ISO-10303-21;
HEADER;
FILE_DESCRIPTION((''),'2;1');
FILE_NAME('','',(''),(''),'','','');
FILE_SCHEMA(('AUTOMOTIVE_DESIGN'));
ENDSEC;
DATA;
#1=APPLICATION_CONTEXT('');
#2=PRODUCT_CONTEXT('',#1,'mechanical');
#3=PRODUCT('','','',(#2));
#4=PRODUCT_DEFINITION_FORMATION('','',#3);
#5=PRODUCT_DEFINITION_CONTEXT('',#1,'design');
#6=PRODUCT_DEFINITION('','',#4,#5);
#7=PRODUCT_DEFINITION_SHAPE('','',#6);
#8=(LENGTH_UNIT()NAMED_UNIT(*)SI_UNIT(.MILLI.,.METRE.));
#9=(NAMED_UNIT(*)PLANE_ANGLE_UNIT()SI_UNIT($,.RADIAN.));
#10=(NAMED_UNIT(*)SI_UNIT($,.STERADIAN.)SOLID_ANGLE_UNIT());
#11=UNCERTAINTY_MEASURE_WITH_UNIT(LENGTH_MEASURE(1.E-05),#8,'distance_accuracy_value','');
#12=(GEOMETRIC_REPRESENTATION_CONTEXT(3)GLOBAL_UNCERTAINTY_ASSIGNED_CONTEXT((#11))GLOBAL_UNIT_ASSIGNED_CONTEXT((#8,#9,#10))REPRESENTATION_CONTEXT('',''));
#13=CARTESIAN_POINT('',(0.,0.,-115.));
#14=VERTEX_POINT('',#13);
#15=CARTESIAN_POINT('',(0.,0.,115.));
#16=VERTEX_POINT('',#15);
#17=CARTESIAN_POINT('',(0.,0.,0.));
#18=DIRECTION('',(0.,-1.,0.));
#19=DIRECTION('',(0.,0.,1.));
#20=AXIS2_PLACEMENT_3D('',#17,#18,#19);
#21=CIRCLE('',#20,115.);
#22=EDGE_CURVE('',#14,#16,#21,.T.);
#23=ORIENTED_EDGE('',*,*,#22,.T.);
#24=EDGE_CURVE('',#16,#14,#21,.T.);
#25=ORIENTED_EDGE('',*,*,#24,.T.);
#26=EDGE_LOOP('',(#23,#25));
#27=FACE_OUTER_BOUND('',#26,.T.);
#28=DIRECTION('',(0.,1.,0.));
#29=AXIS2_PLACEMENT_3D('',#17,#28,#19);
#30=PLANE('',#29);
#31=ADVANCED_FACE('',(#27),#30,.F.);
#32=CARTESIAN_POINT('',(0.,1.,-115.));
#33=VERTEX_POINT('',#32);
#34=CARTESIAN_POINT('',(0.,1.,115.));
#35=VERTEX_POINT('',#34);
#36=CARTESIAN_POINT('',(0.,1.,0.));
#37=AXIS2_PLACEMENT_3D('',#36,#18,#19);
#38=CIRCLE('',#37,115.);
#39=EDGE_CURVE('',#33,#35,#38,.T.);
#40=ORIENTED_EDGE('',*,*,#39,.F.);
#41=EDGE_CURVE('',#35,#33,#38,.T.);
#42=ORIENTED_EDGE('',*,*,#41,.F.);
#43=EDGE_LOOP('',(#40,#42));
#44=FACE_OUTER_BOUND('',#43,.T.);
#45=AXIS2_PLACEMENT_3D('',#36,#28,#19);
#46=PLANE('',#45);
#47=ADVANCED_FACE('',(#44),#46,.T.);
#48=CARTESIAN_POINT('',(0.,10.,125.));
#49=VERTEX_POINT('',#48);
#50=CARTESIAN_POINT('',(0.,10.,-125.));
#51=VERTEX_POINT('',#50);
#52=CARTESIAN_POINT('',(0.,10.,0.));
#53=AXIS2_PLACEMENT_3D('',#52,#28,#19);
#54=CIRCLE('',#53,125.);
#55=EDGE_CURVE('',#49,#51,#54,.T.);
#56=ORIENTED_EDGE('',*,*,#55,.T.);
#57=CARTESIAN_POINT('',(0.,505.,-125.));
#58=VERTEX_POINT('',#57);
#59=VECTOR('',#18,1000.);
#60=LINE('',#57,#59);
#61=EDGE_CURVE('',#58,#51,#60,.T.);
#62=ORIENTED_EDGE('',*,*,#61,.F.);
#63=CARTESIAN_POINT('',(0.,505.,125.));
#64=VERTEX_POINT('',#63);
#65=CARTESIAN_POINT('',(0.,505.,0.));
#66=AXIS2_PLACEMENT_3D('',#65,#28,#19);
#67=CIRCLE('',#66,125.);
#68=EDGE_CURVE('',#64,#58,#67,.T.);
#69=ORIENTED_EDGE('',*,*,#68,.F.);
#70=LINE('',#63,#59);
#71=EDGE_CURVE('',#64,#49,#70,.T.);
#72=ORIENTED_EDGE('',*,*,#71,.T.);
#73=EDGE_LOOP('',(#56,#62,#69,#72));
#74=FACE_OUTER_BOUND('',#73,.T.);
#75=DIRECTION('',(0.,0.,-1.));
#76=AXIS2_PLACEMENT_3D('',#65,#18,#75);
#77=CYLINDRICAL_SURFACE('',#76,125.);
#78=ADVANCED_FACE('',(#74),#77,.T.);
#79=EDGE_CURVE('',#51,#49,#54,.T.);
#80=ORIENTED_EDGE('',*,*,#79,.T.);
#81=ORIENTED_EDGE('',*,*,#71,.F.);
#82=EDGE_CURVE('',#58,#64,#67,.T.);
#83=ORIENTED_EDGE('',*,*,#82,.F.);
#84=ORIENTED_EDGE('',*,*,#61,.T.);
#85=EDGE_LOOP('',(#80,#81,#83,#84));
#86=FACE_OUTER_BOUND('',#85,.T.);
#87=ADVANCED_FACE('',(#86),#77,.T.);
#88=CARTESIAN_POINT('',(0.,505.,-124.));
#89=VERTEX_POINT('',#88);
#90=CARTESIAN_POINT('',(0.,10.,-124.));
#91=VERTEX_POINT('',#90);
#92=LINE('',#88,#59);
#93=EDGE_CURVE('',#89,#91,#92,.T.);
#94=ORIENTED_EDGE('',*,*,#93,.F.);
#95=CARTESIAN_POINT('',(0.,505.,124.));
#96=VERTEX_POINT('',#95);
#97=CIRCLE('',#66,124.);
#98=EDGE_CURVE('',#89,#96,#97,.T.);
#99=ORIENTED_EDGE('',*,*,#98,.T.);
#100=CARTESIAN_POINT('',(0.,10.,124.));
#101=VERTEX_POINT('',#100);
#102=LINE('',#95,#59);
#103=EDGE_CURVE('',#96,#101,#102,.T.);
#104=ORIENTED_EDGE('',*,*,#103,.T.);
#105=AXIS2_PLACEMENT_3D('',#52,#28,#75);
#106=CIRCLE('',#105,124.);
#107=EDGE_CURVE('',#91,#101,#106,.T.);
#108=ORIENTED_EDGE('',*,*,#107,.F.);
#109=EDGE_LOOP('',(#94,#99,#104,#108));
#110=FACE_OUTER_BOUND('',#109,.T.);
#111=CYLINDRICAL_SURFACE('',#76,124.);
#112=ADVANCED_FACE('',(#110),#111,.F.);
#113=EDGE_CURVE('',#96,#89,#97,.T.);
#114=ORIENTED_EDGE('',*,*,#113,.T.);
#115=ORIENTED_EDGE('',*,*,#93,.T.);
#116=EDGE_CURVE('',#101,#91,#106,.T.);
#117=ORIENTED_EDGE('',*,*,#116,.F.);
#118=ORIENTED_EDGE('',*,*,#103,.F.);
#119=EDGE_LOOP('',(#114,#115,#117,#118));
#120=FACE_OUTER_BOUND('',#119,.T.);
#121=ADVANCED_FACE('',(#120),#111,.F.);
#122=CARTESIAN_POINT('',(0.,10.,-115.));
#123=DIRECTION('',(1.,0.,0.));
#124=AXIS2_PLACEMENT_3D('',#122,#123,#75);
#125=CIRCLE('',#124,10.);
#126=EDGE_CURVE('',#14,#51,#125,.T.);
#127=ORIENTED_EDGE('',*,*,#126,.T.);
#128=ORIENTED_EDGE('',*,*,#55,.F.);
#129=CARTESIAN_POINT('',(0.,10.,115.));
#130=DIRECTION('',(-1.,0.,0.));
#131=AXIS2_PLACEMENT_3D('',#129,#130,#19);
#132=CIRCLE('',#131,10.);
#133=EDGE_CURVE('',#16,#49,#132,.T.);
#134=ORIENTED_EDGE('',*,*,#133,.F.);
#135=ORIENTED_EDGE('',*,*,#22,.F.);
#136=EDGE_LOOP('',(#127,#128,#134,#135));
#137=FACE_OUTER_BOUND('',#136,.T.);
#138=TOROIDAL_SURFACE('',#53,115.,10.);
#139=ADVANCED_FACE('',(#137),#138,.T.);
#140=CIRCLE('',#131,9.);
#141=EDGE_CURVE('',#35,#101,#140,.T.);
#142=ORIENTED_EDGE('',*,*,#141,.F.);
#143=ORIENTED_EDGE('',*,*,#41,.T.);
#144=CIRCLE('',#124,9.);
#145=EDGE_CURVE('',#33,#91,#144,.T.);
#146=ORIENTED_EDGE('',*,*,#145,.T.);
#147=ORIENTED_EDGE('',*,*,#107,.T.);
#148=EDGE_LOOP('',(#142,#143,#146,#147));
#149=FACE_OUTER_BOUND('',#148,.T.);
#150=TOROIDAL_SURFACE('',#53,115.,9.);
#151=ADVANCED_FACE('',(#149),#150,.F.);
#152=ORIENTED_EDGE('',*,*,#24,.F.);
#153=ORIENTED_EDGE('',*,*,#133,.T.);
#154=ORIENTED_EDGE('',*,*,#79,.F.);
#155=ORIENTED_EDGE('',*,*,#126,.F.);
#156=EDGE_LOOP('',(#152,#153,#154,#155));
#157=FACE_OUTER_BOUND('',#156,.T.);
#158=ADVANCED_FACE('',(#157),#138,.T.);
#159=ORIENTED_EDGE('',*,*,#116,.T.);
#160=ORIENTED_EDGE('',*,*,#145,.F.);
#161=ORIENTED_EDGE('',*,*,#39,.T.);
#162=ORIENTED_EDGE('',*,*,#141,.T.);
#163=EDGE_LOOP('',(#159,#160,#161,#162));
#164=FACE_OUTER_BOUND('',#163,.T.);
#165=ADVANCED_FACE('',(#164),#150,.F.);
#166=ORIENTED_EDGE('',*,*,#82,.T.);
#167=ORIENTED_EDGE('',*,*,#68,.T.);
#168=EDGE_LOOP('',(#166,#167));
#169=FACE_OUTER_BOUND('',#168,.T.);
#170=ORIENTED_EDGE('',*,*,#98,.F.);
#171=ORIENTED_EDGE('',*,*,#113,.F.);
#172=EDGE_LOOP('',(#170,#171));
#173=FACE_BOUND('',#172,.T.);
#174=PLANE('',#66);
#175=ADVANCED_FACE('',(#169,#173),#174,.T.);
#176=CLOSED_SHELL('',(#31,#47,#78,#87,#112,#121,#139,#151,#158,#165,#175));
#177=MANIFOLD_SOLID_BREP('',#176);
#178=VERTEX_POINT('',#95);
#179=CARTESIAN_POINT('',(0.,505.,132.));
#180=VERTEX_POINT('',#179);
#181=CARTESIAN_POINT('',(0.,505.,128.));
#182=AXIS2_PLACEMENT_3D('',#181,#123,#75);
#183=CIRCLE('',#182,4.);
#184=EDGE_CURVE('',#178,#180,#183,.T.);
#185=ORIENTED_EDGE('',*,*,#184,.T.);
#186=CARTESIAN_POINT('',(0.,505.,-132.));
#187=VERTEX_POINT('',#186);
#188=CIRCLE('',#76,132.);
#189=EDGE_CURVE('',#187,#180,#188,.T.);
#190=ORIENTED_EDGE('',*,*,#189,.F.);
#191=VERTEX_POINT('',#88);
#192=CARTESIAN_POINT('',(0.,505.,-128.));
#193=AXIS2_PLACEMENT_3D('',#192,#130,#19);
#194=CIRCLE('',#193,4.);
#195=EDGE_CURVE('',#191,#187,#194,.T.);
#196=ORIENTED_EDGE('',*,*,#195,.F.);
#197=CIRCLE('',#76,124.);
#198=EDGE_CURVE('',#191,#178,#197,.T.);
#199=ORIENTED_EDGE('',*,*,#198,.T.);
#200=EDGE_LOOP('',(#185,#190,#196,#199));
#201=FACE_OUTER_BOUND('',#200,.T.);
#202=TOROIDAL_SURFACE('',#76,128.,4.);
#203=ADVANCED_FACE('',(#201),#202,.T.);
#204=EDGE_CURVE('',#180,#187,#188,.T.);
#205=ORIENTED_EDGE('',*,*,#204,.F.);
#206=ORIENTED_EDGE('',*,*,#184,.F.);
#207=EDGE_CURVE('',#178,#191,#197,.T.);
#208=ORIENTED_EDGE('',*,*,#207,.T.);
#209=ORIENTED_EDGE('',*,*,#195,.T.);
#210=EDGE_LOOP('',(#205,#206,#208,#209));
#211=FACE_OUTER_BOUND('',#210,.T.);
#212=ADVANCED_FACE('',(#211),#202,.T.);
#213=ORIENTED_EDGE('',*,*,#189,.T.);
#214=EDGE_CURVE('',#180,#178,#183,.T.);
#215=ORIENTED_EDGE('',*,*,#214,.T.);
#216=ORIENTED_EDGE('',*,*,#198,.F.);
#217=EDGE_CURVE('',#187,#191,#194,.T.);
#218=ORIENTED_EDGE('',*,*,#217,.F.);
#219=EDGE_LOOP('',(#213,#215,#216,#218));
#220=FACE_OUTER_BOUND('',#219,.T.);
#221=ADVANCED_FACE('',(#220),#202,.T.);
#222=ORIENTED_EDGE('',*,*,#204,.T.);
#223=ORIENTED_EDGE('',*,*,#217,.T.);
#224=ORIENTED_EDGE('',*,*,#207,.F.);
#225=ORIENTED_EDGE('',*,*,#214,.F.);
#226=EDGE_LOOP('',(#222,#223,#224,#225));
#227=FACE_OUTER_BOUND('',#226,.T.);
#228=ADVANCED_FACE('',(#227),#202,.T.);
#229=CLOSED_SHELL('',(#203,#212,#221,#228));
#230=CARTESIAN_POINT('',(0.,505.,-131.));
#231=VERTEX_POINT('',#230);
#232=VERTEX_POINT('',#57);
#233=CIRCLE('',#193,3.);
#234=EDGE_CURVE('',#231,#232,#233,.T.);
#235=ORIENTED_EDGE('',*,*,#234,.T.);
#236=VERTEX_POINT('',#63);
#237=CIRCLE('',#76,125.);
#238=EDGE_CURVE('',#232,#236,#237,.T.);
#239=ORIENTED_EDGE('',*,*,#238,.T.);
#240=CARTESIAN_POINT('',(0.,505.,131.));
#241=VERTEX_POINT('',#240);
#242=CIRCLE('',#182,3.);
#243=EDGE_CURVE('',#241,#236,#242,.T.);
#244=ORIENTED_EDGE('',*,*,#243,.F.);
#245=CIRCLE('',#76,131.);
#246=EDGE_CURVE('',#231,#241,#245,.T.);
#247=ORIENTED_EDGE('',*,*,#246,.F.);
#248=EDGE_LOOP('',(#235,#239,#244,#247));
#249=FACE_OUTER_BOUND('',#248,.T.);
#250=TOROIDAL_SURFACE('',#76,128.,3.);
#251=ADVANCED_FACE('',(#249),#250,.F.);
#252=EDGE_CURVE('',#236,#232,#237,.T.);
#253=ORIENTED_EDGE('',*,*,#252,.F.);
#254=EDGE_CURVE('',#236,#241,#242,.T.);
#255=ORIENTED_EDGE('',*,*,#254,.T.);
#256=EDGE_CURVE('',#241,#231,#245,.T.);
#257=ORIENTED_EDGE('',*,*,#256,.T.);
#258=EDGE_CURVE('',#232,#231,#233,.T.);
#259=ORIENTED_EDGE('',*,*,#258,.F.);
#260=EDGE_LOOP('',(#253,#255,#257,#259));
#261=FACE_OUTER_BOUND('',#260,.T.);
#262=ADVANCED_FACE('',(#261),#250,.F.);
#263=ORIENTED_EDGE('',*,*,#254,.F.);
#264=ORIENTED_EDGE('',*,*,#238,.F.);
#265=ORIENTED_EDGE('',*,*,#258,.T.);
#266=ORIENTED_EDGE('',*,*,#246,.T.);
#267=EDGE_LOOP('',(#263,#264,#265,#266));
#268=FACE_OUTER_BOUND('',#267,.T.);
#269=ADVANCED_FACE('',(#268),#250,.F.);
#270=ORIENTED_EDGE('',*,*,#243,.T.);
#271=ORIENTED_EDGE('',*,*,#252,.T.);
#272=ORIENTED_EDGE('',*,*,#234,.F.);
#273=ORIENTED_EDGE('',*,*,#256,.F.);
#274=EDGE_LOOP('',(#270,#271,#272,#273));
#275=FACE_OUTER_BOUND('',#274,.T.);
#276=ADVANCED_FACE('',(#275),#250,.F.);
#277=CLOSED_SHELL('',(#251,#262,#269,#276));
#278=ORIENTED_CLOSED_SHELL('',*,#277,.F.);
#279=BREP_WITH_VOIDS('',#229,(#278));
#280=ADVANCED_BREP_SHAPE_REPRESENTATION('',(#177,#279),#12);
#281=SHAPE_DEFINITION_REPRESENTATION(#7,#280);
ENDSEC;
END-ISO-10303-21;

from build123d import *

# Parameters (mm, degrees)
SKETCH1_R           = 125
BOSS_EXTRUDE1_DEPTH = 505
FILLET1_R           = 10
SHELL1_T            = -1
SKETCH6_R           = 4
SKETCH6_R_2         = 3


with BuildPart() as part:
    # Sketch1 → Boss-Extrude1 (new body)
    with BuildSketch(Plane(origin=(0, 0, 0), x_dir=(1, 0, 0), z_dir=(0, 1, 0))):
        with Locations(Location((0, 0, 0), (0, 0, 270))):
            Circle(SKETCH1_R)
    extrude(amount=BOSS_EXTRUDE1_DEPTH)

    # Fillet1
    fillet1_edges = [part.edges().sort_by_distance(p)[0] for p in [
        (0, 0, -125),
    ]]
    fillet(fillet1_edges, radius=FILLET1_R)

    # Shell1
    shell1_openings = [part.faces().sort_by_distance(p)[0] for p in [
        (0, 505, 0),
    ]]
    offset(amount=SHELL1_T, openings=shell1_openings, kind=Kind.INTERSECTION)


with BuildPart() as body_2:
    # Sketch6 → Revolve1 (revolve)
    with BuildSketch(Plane.XY, mode=Mode.PRIVATE) as revolve1_sk:
        with Locations((128, 505)):
            Circle(SKETCH6_R)
        with Locations((128, 505)):
            Circle(SKETCH6_R_2, mode=Mode.SUBTRACT)
    revolve(revolve1_sk.sketch.rotate(Axis((0, 505, 0), (0, 1, 0)), 90), axis=Axis((0, 505, 0), (0, 1, 0)))


solid = Compound([part.part, body_2.part])
